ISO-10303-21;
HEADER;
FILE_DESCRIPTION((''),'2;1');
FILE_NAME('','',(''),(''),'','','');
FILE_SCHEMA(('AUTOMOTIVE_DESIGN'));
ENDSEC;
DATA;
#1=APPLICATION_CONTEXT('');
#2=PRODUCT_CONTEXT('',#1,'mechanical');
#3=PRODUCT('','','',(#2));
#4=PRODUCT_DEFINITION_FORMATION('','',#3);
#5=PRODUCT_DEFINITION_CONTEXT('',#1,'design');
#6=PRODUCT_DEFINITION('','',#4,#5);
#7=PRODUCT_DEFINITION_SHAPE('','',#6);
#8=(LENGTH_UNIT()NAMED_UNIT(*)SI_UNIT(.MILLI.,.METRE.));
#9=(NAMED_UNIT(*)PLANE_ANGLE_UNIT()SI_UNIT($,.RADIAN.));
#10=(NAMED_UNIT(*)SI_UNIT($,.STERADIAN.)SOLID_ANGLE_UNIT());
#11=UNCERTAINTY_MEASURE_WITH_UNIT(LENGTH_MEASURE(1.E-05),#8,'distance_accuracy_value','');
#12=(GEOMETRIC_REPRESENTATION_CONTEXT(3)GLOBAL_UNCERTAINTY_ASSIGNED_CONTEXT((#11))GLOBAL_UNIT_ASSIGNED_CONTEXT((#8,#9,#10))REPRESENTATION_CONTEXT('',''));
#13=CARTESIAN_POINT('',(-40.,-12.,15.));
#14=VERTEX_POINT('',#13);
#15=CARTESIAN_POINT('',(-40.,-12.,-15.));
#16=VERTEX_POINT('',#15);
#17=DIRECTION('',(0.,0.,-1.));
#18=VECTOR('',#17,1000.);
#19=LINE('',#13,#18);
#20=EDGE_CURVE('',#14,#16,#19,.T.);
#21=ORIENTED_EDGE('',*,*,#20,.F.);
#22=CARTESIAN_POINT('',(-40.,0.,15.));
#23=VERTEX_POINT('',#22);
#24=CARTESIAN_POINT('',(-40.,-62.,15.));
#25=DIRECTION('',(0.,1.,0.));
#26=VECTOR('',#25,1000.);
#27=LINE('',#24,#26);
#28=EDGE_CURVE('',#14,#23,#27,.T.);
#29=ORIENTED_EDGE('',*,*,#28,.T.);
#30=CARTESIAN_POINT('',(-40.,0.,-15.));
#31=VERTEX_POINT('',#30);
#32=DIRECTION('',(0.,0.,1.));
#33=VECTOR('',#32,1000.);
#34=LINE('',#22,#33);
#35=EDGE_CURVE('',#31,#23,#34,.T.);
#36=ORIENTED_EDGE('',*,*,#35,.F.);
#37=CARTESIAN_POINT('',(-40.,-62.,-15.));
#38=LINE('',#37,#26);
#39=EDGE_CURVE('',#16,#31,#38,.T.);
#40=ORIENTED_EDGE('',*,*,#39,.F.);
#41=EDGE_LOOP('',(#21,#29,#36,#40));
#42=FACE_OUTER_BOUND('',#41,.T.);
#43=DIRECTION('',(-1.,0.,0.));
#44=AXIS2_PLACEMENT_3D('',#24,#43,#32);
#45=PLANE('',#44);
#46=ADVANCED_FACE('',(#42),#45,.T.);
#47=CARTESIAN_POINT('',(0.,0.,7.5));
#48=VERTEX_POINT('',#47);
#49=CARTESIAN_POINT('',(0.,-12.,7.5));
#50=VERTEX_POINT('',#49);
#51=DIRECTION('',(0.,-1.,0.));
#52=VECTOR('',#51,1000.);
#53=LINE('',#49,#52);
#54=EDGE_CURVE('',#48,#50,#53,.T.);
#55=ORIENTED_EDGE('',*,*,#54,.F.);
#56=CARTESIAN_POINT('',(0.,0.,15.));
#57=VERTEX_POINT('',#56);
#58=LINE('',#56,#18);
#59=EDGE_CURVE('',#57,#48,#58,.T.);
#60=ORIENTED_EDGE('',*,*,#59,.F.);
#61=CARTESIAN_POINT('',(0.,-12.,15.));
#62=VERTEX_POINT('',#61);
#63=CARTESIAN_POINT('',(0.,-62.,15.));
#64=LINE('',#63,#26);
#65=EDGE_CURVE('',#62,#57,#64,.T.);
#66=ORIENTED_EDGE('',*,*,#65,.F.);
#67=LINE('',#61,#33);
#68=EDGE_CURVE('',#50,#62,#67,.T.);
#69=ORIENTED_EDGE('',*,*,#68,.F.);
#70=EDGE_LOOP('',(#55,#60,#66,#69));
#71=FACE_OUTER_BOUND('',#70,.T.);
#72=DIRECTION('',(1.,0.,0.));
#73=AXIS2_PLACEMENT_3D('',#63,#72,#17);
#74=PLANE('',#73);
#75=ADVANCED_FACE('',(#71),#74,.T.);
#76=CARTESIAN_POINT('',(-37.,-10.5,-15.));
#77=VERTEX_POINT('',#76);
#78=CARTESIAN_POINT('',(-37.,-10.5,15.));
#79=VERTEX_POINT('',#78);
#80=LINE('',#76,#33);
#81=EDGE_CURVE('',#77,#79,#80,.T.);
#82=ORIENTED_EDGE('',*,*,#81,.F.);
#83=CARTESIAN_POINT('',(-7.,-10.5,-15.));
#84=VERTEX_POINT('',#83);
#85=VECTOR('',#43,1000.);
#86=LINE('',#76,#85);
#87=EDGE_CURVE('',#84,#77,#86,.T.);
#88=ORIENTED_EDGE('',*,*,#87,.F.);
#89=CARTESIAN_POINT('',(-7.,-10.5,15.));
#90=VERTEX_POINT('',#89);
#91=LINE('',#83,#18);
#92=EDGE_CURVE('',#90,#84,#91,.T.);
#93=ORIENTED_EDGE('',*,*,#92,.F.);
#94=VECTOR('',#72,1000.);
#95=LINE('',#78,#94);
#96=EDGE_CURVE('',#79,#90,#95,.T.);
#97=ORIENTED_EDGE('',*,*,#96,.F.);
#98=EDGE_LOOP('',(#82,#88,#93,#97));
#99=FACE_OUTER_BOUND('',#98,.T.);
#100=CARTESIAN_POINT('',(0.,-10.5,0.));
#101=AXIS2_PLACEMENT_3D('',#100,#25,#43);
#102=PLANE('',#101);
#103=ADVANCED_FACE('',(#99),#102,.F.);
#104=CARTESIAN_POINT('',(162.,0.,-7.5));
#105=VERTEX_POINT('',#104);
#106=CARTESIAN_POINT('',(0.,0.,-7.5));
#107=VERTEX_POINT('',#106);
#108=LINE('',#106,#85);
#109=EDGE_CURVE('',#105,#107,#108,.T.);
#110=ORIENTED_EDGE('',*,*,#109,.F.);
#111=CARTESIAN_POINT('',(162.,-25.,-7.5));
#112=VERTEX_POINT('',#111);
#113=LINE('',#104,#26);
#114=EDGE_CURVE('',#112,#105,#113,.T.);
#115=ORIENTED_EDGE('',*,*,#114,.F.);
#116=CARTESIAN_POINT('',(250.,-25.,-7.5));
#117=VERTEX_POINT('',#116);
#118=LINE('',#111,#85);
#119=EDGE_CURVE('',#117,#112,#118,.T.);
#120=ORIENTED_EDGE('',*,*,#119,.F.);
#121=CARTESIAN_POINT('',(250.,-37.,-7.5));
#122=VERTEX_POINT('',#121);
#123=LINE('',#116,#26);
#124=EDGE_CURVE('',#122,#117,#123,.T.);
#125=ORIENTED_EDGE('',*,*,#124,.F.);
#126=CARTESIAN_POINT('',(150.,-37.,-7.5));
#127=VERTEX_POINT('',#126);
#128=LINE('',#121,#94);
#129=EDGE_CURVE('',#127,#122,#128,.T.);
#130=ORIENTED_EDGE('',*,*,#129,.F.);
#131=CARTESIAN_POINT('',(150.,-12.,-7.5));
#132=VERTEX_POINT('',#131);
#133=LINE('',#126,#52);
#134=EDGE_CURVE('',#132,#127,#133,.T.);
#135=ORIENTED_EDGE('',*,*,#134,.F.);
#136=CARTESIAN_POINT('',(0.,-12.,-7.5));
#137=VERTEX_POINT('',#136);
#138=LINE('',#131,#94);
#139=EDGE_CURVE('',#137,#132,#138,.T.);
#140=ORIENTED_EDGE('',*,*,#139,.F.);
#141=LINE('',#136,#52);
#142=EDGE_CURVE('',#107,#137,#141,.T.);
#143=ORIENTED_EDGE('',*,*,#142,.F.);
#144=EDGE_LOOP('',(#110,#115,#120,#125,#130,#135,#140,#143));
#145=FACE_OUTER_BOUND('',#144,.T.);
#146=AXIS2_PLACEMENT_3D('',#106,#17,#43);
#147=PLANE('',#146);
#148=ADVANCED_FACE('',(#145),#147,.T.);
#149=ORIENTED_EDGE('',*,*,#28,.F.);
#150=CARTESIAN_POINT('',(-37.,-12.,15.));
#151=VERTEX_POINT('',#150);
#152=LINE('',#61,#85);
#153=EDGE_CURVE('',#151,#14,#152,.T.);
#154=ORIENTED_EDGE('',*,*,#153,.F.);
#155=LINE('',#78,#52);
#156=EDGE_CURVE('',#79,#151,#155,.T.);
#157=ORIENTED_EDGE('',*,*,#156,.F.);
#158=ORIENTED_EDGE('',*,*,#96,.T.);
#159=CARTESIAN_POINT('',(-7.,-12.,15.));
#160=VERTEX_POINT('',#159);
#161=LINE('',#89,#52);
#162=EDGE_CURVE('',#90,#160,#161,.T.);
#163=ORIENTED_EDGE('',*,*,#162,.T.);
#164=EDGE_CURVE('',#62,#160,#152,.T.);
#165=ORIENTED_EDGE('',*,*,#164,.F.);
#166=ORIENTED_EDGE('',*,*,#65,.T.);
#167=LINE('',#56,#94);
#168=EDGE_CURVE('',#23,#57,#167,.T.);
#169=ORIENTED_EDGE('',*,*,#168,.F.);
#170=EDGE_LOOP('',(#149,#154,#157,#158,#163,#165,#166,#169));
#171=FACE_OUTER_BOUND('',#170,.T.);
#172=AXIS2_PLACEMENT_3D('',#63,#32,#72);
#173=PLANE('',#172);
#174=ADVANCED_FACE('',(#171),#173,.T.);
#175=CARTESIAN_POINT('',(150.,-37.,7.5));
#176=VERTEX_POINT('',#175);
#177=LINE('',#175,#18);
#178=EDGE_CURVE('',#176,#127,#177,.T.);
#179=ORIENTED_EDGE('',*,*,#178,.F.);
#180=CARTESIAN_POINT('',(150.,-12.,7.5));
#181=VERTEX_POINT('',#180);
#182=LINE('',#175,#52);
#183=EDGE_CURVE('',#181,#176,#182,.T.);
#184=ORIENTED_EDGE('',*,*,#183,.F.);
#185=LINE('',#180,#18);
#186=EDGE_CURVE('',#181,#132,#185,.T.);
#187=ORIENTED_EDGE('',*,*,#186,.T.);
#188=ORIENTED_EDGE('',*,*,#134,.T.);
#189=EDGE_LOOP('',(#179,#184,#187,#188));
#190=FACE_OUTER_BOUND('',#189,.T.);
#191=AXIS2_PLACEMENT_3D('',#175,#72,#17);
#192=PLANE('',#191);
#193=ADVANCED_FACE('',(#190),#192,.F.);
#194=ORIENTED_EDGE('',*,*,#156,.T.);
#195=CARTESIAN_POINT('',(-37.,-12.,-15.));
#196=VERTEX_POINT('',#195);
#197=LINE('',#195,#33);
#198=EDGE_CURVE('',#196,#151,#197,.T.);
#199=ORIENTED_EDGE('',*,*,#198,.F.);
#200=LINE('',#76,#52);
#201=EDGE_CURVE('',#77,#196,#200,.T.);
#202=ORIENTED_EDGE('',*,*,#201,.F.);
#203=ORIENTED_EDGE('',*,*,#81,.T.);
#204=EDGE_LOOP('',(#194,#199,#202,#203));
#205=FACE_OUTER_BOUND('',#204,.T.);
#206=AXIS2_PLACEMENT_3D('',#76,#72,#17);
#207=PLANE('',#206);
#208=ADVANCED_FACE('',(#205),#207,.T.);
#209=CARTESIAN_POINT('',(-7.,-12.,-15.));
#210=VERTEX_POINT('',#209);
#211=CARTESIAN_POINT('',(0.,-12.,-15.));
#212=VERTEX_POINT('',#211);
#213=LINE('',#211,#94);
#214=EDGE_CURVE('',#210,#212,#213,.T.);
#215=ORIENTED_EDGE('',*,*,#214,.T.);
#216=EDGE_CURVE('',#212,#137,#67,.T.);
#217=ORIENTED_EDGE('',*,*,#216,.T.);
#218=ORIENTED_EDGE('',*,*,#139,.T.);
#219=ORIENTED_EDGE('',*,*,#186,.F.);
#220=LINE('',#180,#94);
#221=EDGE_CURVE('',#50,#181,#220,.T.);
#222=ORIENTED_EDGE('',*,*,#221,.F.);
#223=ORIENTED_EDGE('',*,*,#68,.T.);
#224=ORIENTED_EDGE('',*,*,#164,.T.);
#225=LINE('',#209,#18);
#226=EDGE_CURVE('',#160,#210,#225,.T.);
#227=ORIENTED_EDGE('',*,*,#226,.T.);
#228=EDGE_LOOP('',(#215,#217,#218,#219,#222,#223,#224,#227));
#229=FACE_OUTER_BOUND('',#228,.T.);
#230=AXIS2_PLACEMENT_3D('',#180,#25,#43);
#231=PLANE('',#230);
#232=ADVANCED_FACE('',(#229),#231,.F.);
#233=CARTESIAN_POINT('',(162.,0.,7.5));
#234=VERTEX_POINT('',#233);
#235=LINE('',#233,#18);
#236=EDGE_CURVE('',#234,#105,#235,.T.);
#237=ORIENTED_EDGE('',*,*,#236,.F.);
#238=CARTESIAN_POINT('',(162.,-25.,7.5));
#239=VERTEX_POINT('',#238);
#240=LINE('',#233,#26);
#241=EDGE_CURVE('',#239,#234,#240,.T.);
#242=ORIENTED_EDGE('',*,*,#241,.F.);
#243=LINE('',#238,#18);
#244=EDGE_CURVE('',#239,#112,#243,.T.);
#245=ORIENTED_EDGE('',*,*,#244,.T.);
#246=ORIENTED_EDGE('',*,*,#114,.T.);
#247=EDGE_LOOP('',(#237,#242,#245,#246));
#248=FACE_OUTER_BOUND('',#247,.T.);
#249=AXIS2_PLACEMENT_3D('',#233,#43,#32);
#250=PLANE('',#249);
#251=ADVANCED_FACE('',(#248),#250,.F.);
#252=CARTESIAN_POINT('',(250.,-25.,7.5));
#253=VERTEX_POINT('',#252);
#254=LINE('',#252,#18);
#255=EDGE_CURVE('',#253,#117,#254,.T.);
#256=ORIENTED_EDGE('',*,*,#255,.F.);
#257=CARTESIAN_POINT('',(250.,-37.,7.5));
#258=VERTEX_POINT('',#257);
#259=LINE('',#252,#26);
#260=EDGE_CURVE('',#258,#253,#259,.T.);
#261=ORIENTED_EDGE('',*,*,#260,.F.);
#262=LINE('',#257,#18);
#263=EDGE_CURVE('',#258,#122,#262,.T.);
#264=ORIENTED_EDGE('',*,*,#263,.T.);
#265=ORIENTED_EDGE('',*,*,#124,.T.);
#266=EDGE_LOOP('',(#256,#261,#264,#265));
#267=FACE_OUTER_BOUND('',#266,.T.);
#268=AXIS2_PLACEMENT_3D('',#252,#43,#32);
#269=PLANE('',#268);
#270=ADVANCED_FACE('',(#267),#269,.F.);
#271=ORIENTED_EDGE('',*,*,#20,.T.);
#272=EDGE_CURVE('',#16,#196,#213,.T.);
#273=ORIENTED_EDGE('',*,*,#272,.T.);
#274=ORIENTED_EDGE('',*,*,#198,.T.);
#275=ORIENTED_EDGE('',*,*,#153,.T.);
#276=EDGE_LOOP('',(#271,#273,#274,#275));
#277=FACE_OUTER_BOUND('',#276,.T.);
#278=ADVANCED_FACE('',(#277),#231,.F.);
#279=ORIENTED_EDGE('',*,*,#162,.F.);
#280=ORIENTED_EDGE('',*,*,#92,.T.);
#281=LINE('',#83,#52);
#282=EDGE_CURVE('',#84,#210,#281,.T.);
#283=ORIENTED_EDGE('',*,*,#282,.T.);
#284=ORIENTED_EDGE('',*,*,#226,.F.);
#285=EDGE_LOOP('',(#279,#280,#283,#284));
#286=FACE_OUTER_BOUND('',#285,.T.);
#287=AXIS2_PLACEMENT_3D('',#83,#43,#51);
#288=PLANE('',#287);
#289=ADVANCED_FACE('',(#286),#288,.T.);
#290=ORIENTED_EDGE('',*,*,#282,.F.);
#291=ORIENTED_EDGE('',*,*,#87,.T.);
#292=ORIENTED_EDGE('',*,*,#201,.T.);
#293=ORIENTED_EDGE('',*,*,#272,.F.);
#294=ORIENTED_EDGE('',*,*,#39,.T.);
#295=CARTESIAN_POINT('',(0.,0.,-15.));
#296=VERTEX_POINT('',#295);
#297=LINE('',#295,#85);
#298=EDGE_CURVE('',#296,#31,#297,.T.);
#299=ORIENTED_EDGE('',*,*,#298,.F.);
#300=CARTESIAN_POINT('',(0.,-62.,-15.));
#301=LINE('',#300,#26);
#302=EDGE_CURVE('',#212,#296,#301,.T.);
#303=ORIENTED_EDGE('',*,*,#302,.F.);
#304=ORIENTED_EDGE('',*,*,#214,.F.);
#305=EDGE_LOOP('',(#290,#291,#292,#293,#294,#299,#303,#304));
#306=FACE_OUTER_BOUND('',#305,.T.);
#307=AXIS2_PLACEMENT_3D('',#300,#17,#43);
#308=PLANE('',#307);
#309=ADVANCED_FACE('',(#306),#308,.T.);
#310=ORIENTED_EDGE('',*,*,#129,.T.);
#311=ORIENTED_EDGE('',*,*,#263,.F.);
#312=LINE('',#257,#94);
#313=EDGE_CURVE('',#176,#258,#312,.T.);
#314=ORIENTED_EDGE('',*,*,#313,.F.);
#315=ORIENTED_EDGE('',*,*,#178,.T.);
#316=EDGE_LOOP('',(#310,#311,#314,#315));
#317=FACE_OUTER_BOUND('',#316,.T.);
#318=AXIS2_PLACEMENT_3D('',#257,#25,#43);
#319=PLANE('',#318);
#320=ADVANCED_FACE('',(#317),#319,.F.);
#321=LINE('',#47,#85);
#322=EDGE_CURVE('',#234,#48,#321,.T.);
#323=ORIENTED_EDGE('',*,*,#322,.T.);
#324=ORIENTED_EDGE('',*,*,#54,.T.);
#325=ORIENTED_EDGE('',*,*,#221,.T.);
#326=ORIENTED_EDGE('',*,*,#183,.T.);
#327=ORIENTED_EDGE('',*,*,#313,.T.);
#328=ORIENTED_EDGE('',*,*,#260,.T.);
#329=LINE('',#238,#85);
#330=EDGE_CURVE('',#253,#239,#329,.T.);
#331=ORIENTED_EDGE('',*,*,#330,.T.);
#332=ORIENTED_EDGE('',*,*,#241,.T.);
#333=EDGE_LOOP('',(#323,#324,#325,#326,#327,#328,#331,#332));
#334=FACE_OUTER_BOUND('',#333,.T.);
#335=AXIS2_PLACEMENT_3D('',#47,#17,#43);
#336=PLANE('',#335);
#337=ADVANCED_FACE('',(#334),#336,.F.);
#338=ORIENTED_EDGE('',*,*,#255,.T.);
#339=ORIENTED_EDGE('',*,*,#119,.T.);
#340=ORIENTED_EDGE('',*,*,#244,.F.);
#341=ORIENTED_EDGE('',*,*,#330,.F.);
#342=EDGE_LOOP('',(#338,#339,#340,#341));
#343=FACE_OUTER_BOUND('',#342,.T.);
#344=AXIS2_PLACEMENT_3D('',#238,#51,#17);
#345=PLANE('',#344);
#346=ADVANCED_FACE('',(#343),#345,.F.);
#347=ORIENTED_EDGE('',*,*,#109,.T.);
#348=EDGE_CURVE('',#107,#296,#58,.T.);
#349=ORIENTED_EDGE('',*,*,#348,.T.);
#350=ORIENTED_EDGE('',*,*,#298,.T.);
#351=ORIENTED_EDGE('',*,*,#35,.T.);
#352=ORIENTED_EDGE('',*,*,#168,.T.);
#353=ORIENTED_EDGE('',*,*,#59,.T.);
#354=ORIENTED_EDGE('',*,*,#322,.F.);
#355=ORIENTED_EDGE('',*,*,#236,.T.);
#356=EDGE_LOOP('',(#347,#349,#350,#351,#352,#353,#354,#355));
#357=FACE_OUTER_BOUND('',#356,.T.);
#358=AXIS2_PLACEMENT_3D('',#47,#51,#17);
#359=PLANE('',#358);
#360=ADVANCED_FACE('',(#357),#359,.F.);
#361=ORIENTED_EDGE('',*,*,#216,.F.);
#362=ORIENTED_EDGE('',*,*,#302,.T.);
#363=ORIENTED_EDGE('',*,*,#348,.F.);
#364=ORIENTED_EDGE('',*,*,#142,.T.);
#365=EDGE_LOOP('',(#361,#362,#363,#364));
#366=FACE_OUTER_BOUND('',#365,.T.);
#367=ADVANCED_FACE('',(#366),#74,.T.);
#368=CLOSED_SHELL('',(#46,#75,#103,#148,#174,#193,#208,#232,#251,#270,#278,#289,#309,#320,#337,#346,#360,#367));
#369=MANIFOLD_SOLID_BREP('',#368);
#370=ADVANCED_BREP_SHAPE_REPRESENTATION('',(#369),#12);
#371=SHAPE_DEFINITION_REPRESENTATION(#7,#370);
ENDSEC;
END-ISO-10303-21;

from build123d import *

# Parameters (mm, degrees)
EXTRUDE_5_DEPTH     = 7.5
SKETCH_7_W          = 40
SKETCH_7_H          = 30
EXTRUDE_6_DEPTH     = 12
SKETCH_8_W          = 30
SKETCH_8_H          = 30
CUT_EXTRUDE_1_DEPTH = 1.5


with BuildPart() as part:
    # 草图6 → 凸台-拉伸5 (new, symmetric)
    with BuildSketch(Plane.XY):
        Polygon((0, 0), (162, 0), (162, -25), (250, -25), (250, -37), (150, -37), (150, -12), (0, -12), align=None)
    extrude(amount=EXTRUDE_5_DEPTH, both=True)

    # 草图7 → 凸台-拉伸6 (add)
    with BuildSketch(Plane(origin=(0, 0, 0), x_dir=(1, 0, 0), z_dir=(0, 1, 0))):
        with Locations((-20, 0)):
            Rectangle(SKETCH_7_W, SKETCH_7_H)
    extrude(amount=-EXTRUDE_6_DEPTH)

    # 草图8 → 切除-拉伸1 (cut)
    with BuildSketch(Plane(origin=(0, -12, 0), x_dir=(1, 0, 0), z_dir=(0, 1, 0))):
        with Locations((-22, 0)):
            Rectangle(SKETCH_8_W, SKETCH_8_H)
    extrude(amount=CUT_EXTRUDE_1_DEPTH, mode=Mode.SUBTRACT)


solid = part.part
